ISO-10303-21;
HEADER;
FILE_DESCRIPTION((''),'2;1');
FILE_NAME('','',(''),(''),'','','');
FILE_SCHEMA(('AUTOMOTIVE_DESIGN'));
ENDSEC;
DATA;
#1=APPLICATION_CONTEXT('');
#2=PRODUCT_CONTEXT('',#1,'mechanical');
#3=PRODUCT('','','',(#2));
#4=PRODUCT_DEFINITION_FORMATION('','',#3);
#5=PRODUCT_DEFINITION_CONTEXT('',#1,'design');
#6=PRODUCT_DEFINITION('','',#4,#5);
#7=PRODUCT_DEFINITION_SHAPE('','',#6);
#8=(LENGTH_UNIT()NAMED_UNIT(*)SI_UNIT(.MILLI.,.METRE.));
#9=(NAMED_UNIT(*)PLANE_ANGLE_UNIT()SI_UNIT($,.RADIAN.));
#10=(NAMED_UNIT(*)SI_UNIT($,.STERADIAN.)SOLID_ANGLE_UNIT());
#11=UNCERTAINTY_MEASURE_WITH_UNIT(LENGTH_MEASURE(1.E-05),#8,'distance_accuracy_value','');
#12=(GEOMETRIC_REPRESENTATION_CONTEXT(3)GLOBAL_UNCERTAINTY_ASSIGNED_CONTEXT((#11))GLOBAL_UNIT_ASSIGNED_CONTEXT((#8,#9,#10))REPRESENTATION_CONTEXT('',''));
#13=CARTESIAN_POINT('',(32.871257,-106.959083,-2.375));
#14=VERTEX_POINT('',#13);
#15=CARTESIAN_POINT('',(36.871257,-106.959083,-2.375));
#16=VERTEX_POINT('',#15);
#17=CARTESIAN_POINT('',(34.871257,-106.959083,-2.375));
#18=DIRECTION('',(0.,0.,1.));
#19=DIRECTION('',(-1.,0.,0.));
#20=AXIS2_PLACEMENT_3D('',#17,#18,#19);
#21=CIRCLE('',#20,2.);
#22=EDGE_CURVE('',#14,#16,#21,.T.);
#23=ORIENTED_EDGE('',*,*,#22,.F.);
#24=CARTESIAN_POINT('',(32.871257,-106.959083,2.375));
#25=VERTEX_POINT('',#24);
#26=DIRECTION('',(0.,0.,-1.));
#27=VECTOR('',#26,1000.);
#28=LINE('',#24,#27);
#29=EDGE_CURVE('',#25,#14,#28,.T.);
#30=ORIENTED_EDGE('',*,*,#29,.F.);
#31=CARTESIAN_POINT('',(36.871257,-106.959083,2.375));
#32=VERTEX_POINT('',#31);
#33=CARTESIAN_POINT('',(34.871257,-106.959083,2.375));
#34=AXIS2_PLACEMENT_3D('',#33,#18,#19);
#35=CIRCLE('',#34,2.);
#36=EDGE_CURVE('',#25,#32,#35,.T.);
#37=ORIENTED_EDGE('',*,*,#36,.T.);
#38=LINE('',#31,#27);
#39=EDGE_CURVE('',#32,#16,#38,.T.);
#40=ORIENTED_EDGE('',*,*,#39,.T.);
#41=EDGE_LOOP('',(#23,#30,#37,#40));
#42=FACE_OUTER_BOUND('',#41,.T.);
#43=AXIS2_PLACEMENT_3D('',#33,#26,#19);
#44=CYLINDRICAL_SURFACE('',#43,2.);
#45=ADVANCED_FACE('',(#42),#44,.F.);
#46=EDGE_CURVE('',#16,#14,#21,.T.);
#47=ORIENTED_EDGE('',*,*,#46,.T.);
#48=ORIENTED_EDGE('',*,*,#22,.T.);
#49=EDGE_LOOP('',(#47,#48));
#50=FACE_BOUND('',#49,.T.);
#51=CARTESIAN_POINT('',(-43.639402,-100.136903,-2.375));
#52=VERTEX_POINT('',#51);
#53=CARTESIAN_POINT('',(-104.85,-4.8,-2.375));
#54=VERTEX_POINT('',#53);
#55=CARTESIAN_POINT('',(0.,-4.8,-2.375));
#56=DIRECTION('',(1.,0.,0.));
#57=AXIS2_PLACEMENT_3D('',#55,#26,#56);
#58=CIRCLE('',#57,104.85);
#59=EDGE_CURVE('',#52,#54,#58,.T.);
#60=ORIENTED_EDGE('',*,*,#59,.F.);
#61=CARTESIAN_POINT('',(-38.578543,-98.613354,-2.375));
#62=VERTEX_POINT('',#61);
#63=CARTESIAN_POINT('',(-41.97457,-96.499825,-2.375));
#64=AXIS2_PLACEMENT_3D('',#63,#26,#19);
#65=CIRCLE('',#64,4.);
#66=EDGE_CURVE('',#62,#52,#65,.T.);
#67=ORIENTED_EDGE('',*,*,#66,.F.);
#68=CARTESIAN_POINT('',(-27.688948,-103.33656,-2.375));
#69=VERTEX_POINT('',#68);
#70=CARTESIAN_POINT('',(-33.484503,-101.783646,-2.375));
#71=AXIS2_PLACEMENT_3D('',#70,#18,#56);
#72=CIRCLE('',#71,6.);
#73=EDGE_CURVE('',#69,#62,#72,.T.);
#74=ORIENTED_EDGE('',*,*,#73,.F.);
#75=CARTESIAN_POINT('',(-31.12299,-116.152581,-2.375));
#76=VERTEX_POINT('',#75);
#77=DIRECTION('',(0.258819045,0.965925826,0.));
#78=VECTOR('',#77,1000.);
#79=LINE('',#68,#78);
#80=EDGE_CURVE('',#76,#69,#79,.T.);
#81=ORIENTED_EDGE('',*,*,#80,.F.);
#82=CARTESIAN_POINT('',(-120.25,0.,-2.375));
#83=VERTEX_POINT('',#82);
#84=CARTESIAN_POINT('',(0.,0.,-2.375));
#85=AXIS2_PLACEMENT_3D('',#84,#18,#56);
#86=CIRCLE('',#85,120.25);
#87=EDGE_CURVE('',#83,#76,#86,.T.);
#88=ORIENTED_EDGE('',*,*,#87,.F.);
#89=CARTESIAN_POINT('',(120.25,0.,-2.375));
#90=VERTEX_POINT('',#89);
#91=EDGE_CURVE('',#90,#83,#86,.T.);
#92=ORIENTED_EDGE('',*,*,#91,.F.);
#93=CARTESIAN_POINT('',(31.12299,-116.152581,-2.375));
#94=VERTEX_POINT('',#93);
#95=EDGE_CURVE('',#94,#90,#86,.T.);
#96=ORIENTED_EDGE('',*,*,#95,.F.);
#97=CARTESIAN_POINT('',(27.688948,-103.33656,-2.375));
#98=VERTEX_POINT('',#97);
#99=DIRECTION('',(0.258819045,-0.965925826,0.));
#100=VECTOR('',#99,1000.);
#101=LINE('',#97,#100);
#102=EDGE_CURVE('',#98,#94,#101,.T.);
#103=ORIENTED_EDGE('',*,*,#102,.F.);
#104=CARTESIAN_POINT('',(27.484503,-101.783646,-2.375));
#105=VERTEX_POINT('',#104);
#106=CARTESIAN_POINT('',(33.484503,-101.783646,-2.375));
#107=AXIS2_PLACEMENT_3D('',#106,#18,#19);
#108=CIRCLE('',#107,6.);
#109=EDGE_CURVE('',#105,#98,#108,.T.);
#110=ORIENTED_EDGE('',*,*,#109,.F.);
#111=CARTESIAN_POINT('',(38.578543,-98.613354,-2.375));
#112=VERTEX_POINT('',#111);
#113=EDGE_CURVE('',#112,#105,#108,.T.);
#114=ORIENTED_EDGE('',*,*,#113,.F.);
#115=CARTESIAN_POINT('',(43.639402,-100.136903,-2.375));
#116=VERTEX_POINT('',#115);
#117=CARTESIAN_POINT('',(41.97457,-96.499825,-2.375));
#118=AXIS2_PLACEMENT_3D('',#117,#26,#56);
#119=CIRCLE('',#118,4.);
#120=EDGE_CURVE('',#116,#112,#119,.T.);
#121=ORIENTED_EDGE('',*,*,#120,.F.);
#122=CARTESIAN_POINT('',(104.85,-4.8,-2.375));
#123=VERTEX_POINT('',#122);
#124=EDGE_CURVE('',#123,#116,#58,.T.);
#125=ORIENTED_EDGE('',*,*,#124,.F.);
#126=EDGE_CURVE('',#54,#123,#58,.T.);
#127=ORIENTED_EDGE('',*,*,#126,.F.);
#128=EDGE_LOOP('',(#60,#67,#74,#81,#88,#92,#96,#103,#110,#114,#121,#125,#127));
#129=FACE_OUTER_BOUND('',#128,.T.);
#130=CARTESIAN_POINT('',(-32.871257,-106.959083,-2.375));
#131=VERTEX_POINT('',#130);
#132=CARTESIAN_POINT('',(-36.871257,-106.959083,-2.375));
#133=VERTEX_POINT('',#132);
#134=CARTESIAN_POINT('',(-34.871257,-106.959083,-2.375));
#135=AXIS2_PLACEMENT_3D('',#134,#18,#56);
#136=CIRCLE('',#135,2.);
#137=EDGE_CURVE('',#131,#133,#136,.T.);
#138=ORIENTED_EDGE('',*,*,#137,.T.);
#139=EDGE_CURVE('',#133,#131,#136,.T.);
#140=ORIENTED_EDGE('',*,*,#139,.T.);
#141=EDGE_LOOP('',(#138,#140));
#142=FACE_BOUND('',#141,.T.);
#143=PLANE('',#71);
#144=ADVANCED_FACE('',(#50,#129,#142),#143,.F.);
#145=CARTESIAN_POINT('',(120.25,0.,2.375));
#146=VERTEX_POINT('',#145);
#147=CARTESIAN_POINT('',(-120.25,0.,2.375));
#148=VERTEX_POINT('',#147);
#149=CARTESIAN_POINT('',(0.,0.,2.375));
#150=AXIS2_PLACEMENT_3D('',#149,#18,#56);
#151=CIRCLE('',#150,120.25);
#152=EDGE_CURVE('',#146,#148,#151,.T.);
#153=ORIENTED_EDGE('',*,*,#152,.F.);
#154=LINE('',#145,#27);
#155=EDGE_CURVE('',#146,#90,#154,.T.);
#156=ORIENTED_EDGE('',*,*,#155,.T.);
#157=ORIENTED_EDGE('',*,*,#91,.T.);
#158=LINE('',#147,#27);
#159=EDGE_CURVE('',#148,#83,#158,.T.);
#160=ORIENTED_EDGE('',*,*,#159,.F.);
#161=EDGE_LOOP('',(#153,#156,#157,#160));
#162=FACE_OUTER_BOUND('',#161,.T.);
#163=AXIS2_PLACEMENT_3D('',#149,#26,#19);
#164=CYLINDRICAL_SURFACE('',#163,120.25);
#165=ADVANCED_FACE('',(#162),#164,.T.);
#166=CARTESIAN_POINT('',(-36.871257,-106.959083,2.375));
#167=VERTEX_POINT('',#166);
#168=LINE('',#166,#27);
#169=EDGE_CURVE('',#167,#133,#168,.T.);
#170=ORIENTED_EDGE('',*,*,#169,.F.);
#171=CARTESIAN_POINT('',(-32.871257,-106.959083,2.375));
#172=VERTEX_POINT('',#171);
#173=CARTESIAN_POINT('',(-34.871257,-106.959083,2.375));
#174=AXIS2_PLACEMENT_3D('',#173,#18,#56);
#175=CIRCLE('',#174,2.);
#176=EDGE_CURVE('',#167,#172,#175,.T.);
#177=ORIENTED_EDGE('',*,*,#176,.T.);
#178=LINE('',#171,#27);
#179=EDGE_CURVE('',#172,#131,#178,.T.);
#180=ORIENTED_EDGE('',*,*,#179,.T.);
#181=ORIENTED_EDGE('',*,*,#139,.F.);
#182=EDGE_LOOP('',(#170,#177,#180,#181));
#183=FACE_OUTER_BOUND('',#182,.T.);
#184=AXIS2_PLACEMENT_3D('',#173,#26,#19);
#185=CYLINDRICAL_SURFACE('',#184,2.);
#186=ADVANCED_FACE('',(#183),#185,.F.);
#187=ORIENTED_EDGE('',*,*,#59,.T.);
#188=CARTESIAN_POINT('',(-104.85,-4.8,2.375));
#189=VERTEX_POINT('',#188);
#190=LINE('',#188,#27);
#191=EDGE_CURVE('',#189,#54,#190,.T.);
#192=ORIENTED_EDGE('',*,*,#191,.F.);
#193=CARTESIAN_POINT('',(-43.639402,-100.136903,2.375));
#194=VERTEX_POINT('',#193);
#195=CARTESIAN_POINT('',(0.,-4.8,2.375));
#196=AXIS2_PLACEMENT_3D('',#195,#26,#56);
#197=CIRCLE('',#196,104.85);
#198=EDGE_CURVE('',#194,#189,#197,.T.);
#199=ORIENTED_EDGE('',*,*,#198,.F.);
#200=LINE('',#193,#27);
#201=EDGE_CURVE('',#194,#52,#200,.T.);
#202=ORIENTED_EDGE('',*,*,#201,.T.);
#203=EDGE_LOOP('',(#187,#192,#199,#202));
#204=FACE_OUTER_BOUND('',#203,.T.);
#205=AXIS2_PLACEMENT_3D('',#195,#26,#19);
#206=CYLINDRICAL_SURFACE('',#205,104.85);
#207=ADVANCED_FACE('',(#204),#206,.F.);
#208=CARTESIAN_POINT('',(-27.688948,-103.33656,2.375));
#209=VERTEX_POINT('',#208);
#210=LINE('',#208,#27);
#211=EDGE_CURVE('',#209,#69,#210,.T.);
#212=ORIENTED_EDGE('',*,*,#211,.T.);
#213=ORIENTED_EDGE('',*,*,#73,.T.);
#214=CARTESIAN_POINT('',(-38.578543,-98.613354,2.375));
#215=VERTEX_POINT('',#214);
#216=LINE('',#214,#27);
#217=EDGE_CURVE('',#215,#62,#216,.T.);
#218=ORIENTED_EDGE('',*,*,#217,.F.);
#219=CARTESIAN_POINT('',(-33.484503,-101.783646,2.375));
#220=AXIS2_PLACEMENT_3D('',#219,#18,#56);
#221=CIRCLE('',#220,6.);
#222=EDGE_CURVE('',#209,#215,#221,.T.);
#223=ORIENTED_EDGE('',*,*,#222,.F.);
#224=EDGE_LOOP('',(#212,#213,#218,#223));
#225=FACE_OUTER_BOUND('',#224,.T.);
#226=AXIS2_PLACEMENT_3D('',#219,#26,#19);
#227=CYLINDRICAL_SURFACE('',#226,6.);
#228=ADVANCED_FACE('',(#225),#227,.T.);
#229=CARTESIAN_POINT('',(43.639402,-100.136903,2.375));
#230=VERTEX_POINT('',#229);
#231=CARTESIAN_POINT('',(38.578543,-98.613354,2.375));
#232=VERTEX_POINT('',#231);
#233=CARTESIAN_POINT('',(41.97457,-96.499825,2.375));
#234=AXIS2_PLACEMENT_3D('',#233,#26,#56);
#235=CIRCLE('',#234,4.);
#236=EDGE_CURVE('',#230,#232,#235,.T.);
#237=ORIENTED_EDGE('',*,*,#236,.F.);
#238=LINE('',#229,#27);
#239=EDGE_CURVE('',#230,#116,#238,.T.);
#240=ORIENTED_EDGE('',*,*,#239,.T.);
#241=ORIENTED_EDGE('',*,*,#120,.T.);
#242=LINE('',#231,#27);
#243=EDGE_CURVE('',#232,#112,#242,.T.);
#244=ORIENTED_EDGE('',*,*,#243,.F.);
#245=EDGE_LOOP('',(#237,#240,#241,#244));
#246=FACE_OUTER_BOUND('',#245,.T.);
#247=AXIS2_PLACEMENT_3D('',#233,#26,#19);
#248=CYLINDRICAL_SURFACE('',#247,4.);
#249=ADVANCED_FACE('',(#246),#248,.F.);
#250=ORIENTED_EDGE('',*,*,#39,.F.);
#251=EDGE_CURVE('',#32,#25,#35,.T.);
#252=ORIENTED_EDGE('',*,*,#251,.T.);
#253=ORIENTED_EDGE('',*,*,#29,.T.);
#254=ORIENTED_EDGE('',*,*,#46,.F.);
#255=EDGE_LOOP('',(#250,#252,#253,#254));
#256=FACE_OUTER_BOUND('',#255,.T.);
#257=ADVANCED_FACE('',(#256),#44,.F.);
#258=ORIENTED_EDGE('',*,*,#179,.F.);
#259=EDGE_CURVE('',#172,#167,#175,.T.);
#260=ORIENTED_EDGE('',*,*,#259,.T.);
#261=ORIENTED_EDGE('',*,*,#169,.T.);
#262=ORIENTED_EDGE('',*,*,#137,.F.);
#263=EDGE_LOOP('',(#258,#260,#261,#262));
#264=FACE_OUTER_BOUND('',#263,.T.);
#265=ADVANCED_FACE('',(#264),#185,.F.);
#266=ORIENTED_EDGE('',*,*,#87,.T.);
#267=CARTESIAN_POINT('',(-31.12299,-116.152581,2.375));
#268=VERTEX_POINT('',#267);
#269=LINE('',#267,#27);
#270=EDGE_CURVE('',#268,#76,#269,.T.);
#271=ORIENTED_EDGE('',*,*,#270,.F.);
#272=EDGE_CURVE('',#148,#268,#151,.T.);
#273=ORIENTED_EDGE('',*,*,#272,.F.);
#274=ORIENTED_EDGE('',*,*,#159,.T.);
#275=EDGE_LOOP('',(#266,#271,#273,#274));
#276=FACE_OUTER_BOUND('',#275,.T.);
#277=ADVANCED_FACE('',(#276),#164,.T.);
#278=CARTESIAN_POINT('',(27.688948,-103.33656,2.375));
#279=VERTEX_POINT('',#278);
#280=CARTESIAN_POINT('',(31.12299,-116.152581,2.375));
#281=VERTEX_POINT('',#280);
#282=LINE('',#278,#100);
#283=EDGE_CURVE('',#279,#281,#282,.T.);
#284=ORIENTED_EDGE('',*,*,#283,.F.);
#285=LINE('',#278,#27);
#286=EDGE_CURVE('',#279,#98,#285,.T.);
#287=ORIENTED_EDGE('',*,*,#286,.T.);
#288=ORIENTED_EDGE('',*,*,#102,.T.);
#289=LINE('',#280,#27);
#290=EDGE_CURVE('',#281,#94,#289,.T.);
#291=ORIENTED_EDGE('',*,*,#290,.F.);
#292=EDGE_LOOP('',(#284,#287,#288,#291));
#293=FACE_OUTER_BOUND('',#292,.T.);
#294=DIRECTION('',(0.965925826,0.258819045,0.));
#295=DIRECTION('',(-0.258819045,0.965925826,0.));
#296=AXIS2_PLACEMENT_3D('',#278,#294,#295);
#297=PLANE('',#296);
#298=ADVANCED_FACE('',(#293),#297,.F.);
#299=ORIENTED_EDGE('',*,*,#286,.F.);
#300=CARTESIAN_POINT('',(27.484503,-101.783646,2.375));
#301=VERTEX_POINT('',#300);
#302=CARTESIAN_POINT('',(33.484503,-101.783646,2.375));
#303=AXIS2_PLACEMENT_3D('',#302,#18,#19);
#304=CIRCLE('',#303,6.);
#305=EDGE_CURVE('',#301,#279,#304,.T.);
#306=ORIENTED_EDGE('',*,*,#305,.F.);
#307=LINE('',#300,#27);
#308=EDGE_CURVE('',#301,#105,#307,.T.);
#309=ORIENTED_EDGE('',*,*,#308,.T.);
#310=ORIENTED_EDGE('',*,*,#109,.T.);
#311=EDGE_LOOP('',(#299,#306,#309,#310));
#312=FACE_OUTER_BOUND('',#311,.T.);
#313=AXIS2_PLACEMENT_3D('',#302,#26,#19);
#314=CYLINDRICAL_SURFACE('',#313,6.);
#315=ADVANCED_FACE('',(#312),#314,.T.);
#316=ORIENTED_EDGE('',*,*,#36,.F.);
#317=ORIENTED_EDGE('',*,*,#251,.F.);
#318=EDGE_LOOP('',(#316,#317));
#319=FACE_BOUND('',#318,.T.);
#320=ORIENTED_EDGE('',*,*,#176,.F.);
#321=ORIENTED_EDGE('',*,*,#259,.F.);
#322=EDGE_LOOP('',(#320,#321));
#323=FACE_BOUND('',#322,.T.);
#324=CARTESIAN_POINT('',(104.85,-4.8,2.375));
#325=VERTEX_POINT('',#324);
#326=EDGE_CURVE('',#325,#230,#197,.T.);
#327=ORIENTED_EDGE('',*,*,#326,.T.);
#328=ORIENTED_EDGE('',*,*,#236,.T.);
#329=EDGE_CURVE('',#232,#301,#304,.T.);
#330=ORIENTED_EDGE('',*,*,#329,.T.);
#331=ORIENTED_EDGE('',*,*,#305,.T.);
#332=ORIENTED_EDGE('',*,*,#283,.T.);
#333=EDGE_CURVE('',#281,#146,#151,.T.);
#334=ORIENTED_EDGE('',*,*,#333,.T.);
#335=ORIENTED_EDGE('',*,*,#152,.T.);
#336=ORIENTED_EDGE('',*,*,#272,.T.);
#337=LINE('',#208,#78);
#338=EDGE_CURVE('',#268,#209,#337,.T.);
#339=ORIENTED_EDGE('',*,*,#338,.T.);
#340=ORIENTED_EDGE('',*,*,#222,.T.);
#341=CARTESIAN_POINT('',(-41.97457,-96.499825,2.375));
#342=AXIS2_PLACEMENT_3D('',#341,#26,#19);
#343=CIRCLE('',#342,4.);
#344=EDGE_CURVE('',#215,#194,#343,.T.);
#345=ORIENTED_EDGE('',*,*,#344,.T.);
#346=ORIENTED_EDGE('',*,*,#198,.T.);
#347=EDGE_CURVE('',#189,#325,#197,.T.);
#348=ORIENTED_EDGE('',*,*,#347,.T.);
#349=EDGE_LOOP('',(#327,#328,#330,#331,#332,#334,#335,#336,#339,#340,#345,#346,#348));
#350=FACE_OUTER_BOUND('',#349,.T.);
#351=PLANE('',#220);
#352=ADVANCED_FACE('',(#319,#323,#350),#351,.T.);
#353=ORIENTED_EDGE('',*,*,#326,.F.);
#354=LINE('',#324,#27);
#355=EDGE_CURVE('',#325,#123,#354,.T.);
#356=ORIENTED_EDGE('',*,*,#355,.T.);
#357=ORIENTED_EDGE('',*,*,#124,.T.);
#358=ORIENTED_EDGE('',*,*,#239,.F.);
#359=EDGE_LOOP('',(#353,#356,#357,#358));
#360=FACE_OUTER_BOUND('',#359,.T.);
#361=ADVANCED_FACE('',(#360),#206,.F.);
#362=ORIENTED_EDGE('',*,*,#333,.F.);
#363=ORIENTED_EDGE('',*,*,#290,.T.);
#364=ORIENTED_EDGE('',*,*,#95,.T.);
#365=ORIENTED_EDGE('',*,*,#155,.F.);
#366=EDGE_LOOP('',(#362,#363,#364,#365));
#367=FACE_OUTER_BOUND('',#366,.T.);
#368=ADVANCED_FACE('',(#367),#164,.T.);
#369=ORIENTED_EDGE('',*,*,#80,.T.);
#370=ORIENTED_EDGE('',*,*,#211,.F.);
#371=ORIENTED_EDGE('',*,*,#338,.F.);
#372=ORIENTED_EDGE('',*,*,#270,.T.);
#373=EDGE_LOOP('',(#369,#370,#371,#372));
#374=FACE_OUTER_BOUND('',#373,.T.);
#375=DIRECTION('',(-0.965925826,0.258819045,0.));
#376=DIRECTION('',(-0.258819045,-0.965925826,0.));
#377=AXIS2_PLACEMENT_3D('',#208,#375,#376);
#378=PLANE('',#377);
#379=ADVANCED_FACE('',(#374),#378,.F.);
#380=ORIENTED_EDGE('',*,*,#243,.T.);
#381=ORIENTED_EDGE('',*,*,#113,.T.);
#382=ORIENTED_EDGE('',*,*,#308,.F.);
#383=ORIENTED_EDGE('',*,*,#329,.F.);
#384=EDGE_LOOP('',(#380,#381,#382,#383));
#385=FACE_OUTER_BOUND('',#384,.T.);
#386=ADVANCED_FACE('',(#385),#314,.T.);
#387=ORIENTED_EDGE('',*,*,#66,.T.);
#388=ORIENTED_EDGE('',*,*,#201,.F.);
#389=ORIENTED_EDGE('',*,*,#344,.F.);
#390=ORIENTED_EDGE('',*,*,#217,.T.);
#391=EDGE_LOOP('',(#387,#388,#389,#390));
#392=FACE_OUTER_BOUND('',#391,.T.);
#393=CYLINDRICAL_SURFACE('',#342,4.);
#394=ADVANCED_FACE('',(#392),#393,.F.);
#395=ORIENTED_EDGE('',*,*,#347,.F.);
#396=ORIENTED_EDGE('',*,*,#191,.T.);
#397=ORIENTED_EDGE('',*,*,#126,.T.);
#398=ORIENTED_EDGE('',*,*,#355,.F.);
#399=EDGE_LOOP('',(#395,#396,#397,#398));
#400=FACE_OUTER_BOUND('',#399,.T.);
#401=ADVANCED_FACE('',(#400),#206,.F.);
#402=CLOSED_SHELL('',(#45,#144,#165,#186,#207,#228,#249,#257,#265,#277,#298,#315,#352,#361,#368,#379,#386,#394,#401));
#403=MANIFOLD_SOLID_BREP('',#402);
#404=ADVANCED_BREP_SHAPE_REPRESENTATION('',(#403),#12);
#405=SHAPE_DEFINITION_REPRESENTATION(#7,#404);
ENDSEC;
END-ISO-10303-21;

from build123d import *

# Parameters (mm, degrees)
SKETCH1_R          = 2
BASE_EXTRUDE_DEPTH = 2.375


with BuildPart() as part:
    # Sketch1 → Base-Extrude (new, symmetric)
    with BuildSketch(Plane.XY):
        with BuildLine():
            Line((-27.688947845, -103.336560167), (-31.122990174, -116.152580611))
            ThreePointArc((-31.122990174, -116.152580611), (0, 120.25), (31.122990174, -116.152580611))
            Line((31.122990174, -116.152580611), (27.688947845, -103.336560167))
            ThreePointArc((27.688947845, -103.336560167), (31.096993473, -96.279120559), (38.578543112, -98.613353586))
            ThreePointArc((38.578543112, -98.613353586), (40.821504489, -100.330026414), (43.639401714, -100.136903233))
            ThreePointArc((43.639401714, -100.136903233), (0, 100.05), (-43.639401714, -100.136903233))
            ThreePointArc((-43.639401714, -100.136903233), (-40.821504489, -100.330026414), (-38.578543112, -98.613353586))
            ThreePointArc((-38.578543112, -98.613353586), (-31.096993473, -96.279120559), (-27.688947845, -103.336560167))
        make_face()
        with Locations((-34.871256995, -106.959082997)):
            Circle(SKETCH1_R, mode=Mode.SUBTRACT)
        with Locations(Location((34.871256995, -106.959082997, 0), (0, 0, 180))):
            Circle(SKETCH1_R, mode=Mode.SUBTRACT)
    extrude(amount=BASE_EXTRUDE_DEPTH, both=True)


solid = part.part
